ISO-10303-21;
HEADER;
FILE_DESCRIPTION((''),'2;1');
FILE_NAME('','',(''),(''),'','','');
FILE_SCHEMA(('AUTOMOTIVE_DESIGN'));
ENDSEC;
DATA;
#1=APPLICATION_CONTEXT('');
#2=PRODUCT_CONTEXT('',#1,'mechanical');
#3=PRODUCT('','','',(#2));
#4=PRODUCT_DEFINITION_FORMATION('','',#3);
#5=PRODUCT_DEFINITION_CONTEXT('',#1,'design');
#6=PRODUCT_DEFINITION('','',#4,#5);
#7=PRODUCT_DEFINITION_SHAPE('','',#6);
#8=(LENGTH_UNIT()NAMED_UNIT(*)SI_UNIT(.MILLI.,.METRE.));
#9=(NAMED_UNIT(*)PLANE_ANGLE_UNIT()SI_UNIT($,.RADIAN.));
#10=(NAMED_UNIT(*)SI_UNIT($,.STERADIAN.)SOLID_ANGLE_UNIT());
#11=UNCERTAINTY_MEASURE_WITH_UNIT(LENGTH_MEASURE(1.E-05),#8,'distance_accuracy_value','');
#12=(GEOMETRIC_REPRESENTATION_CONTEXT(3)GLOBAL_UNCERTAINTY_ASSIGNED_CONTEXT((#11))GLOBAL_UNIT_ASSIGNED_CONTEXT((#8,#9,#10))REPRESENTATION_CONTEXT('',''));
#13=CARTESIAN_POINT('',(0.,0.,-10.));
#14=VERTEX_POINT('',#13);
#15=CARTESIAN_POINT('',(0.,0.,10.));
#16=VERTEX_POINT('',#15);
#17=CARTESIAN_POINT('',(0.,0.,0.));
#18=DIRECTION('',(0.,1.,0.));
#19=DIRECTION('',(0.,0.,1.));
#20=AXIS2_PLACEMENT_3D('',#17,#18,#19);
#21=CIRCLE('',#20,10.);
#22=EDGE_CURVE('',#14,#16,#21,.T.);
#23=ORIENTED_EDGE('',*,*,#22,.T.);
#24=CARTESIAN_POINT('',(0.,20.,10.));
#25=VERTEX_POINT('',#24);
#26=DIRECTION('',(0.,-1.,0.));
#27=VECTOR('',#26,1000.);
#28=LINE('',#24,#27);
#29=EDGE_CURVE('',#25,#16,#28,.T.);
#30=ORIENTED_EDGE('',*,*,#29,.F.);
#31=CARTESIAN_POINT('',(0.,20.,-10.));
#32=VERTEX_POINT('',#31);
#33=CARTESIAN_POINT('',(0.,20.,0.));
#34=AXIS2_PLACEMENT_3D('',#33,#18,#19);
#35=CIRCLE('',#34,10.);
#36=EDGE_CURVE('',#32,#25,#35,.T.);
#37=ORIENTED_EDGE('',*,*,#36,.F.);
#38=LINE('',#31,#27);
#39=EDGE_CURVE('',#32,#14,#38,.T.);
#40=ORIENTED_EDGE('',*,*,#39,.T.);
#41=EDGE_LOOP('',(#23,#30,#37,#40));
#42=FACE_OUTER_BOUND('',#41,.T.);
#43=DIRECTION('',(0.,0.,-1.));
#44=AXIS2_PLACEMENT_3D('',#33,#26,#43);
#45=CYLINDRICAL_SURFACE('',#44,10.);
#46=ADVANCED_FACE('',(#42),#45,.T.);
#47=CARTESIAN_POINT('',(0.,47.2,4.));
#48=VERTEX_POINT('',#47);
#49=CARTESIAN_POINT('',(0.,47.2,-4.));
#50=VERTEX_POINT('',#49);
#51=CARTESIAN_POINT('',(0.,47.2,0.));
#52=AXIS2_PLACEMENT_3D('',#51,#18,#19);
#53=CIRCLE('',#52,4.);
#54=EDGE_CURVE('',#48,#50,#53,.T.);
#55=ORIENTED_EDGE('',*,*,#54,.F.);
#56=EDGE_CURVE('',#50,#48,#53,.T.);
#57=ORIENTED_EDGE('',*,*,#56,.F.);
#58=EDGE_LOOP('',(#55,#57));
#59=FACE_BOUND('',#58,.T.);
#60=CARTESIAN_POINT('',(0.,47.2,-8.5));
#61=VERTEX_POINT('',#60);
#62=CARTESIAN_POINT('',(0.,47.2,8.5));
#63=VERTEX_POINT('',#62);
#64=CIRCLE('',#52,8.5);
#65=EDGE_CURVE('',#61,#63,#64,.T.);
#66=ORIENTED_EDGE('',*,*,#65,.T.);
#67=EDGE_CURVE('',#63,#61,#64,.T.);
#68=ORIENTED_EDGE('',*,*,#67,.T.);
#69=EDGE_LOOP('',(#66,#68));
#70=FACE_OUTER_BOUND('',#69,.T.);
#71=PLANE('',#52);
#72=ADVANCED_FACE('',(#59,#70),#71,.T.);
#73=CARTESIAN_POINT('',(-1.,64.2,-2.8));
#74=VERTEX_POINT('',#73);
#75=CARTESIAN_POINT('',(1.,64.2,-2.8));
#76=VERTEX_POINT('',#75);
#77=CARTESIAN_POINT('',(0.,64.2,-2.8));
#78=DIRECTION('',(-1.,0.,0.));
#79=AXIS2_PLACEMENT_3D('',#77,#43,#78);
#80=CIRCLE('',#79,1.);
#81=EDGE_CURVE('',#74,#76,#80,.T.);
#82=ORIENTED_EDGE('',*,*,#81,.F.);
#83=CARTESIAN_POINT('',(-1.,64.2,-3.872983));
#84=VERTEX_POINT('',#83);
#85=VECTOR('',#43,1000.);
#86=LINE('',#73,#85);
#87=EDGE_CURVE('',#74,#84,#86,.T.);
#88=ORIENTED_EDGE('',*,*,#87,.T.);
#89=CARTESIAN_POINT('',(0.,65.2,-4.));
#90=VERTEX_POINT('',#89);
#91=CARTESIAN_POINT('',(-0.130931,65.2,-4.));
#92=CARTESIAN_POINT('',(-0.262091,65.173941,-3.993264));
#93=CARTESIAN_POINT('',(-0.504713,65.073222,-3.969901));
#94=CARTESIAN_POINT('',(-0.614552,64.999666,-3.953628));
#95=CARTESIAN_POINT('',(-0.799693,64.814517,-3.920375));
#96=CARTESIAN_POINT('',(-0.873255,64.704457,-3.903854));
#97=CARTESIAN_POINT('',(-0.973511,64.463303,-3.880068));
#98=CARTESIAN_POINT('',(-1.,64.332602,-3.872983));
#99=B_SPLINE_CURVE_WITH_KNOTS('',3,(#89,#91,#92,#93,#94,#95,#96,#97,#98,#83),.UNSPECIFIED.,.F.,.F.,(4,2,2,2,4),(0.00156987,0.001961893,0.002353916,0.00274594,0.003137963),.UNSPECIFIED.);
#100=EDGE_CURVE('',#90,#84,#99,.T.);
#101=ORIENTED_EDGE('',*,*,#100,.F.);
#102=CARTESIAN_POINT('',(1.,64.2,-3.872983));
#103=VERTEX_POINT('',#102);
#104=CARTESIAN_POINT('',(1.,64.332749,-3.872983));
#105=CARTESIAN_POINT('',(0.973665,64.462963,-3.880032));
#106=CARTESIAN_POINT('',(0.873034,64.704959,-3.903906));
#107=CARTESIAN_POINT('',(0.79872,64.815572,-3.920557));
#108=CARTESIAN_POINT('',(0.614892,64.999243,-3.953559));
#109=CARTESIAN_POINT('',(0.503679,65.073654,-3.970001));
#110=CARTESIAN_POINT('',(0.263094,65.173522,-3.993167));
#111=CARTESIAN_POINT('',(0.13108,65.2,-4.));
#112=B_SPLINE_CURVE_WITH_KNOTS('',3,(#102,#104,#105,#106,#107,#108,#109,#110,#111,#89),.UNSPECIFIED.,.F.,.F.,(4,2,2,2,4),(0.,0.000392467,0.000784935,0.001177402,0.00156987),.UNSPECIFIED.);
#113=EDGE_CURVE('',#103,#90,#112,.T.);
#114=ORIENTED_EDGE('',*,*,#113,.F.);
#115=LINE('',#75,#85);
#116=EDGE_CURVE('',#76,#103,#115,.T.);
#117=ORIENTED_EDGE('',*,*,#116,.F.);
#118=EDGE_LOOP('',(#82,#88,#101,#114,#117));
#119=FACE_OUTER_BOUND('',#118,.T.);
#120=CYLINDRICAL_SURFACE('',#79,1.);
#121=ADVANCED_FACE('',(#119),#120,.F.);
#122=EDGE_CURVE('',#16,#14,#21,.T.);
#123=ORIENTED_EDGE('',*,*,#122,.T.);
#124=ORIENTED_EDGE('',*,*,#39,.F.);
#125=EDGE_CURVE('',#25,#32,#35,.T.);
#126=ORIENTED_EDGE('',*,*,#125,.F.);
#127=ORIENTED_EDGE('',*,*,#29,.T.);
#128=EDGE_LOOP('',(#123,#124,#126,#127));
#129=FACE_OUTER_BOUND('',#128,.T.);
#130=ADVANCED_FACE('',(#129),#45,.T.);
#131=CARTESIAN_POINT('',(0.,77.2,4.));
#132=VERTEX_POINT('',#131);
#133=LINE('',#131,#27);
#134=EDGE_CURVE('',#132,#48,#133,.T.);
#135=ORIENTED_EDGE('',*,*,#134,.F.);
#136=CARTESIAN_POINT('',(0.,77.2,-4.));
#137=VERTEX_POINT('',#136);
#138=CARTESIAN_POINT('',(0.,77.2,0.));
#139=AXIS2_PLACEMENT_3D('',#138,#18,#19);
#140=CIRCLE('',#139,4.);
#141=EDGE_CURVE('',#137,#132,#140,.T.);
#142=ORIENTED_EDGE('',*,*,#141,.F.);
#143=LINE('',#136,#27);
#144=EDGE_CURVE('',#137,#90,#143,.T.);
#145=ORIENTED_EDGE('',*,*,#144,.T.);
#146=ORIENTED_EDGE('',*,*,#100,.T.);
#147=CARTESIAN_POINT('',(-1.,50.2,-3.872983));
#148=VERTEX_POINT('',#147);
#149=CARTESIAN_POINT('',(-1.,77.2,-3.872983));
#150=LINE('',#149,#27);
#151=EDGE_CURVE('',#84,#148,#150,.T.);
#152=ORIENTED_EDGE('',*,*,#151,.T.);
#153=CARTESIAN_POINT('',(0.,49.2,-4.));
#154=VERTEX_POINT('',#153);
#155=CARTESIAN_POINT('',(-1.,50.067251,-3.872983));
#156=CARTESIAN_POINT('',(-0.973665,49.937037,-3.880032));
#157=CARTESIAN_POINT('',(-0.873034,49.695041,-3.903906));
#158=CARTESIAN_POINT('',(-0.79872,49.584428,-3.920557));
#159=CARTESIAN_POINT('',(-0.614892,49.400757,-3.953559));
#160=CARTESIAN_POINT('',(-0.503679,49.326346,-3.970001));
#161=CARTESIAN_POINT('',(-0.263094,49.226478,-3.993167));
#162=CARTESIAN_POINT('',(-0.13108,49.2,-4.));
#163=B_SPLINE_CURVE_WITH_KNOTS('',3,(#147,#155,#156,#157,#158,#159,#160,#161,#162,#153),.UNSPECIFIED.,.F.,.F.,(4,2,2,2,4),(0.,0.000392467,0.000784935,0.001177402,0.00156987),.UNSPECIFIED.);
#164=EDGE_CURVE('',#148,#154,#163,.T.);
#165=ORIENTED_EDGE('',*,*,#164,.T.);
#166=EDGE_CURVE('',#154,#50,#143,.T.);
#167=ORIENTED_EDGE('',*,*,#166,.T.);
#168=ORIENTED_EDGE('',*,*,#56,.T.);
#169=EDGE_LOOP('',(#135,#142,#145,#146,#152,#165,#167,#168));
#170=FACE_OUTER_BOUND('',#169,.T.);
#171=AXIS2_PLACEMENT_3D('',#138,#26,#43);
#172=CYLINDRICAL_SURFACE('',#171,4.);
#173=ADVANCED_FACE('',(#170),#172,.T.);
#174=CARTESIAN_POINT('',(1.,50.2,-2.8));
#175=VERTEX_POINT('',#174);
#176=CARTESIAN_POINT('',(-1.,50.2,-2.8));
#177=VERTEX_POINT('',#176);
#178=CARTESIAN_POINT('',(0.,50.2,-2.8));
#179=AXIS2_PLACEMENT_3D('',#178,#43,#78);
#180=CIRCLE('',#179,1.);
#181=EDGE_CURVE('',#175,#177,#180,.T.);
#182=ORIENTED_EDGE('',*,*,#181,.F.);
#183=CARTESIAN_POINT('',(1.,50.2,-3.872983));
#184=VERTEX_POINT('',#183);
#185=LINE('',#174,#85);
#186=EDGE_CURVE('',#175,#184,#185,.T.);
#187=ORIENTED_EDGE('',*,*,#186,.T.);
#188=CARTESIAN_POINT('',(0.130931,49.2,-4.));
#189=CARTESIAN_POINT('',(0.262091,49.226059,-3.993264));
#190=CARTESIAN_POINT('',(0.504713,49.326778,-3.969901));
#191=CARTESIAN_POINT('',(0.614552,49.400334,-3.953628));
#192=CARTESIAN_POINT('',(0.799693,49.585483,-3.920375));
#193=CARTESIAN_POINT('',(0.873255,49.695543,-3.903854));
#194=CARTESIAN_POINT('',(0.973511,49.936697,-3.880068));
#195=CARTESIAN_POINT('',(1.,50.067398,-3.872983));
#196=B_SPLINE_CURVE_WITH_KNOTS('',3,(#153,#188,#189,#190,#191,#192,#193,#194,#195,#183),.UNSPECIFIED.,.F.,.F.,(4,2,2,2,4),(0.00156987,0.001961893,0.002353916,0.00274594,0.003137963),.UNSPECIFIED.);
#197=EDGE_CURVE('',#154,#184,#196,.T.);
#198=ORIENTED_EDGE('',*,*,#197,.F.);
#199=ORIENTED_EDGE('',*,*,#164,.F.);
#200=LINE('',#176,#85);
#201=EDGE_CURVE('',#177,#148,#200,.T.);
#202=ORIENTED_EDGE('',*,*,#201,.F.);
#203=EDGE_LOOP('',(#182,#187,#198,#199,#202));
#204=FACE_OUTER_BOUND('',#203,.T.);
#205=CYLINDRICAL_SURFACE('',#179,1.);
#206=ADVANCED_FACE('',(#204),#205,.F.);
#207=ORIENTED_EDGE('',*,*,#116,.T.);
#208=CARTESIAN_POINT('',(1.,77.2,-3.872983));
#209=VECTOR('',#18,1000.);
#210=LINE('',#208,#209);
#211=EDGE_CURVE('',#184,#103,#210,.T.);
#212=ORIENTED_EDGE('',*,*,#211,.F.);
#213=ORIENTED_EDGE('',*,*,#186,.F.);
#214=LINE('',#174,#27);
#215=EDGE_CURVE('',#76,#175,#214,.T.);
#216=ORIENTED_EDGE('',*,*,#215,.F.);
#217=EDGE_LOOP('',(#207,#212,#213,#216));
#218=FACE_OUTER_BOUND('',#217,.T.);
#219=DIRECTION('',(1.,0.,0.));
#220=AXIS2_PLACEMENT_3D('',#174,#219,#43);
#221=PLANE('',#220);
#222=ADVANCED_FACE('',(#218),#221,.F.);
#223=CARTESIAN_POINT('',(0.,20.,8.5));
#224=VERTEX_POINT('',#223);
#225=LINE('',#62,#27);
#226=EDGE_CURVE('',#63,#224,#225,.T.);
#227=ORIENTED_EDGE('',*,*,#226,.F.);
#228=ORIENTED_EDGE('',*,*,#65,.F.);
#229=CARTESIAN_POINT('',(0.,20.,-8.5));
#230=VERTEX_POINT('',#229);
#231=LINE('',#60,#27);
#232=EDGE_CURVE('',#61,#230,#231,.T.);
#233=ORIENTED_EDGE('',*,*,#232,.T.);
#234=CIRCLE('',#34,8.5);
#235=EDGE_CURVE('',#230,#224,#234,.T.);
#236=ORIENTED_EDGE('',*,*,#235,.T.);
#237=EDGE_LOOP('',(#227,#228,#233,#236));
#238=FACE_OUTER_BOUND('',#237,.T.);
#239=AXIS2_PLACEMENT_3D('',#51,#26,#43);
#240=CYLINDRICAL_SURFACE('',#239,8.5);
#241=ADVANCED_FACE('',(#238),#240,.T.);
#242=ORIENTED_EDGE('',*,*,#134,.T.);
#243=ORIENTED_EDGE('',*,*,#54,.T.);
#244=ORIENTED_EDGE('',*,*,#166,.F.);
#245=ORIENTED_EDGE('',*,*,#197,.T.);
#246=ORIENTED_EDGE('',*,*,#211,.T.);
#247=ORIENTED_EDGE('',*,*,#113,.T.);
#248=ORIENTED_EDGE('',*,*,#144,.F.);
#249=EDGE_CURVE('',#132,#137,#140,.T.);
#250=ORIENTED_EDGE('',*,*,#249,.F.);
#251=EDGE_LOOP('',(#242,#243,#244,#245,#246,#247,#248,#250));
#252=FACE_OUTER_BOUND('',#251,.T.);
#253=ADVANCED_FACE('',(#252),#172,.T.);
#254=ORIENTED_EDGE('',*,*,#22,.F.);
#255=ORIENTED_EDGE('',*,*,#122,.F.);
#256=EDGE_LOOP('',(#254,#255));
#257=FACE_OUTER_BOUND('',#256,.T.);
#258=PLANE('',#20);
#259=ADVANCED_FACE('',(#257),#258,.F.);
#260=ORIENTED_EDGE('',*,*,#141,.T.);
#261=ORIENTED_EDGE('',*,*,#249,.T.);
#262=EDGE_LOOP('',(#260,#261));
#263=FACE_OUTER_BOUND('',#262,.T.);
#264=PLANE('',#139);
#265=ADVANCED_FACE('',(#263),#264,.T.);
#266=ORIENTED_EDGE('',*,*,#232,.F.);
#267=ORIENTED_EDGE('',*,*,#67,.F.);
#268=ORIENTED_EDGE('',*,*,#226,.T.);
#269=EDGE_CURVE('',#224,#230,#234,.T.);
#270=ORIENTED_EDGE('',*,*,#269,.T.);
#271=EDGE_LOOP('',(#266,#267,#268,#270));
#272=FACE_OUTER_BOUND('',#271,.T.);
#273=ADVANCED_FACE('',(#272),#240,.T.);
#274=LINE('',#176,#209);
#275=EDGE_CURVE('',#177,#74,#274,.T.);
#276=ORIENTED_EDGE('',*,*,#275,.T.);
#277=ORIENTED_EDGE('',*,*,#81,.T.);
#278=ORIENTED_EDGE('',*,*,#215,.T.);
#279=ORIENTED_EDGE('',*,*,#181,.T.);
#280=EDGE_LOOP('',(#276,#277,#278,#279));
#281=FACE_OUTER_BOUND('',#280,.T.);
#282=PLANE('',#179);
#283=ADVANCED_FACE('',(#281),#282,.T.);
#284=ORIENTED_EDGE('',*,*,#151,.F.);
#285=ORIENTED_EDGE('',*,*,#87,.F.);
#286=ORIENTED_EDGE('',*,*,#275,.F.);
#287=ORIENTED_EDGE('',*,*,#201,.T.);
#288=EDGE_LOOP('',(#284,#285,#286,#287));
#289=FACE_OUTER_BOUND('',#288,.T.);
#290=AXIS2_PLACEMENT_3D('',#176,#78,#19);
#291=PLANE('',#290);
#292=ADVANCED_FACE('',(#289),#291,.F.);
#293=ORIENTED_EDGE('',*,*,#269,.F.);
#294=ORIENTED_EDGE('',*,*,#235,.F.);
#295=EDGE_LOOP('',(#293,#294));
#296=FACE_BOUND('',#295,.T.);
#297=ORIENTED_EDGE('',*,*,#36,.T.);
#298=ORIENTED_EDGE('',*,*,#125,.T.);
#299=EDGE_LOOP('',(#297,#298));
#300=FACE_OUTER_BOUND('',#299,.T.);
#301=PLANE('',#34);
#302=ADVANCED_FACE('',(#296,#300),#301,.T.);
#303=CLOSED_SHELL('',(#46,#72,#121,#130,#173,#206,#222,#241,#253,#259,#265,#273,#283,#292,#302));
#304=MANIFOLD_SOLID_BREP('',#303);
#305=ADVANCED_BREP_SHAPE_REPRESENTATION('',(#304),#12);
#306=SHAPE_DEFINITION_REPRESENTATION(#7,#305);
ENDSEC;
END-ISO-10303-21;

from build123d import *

# Parameters (mm, degrees)
SKETCH1_R           = 10
BOSS_EXTRUDE1_DEPTH = 20
SKETCH2_R           = 8.5
BOSS_EXTRUDE2_DEPTH = 27.2
SKETCH3_R           = 4
BOSS_EXTRUDE3_DEPTH = 30
CUT_EXTRUDE1_DEPTH  = 1.2


with BuildPart() as part:
    # Sketch1 → Boss-Extrude1 (new body)
    with BuildSketch(Plane(origin=(0, 0, 0), x_dir=(1, 0, 0), z_dir=(0, 1, 0))):
        with Locations(Location((0, 0, 0), (0, 0, 270))):
            Circle(SKETCH1_R)
    extrude(amount=BOSS_EXTRUDE1_DEPTH)

    # Sketch2 → Boss-Extrude2 (add)
    with BuildSketch(Plane(origin=(0, 20, 0), x_dir=(1, 0, 0), z_dir=(0, 1, 0))):
        with Locations(Location((0, 0, 0), (0, 0, 270))):
            Circle(SKETCH2_R)
    extrude(amount=BOSS_EXTRUDE2_DEPTH)

    # Sketch3 → Boss-Extrude3 (add)
    with BuildSketch(Plane(origin=(0, 47.2, 0), x_dir=(1, 0, 0), z_dir=(0, 1, 0))):
        with Locations(Location((0, 0, 0), (0, 0, 270))):
            Circle(SKETCH3_R)
    extrude(amount=BOSS_EXTRUDE3_DEPTH)

    # Sketch4 → Cut-Extrude1 (cut)
    with BuildSketch(Plane(origin=(0, 0, -4), x_dir=(-1, 0, 0), z_dir=(0, 0, -1))):
        with BuildLine():
            Line((-1, 50.2), (-1, 64.2))
            ThreePointArc((-1, 64.2), (0, 65.2), (1, 64.2))
            Line((1, 64.2), (1, 50.2))
            ThreePointArc((1, 50.2), (0, 49.2), (-1, 50.2))
        make_face()
    extrude(amount=-CUT_EXTRUDE1_DEPTH, mode=Mode.SUBTRACT)


solid = part.part
